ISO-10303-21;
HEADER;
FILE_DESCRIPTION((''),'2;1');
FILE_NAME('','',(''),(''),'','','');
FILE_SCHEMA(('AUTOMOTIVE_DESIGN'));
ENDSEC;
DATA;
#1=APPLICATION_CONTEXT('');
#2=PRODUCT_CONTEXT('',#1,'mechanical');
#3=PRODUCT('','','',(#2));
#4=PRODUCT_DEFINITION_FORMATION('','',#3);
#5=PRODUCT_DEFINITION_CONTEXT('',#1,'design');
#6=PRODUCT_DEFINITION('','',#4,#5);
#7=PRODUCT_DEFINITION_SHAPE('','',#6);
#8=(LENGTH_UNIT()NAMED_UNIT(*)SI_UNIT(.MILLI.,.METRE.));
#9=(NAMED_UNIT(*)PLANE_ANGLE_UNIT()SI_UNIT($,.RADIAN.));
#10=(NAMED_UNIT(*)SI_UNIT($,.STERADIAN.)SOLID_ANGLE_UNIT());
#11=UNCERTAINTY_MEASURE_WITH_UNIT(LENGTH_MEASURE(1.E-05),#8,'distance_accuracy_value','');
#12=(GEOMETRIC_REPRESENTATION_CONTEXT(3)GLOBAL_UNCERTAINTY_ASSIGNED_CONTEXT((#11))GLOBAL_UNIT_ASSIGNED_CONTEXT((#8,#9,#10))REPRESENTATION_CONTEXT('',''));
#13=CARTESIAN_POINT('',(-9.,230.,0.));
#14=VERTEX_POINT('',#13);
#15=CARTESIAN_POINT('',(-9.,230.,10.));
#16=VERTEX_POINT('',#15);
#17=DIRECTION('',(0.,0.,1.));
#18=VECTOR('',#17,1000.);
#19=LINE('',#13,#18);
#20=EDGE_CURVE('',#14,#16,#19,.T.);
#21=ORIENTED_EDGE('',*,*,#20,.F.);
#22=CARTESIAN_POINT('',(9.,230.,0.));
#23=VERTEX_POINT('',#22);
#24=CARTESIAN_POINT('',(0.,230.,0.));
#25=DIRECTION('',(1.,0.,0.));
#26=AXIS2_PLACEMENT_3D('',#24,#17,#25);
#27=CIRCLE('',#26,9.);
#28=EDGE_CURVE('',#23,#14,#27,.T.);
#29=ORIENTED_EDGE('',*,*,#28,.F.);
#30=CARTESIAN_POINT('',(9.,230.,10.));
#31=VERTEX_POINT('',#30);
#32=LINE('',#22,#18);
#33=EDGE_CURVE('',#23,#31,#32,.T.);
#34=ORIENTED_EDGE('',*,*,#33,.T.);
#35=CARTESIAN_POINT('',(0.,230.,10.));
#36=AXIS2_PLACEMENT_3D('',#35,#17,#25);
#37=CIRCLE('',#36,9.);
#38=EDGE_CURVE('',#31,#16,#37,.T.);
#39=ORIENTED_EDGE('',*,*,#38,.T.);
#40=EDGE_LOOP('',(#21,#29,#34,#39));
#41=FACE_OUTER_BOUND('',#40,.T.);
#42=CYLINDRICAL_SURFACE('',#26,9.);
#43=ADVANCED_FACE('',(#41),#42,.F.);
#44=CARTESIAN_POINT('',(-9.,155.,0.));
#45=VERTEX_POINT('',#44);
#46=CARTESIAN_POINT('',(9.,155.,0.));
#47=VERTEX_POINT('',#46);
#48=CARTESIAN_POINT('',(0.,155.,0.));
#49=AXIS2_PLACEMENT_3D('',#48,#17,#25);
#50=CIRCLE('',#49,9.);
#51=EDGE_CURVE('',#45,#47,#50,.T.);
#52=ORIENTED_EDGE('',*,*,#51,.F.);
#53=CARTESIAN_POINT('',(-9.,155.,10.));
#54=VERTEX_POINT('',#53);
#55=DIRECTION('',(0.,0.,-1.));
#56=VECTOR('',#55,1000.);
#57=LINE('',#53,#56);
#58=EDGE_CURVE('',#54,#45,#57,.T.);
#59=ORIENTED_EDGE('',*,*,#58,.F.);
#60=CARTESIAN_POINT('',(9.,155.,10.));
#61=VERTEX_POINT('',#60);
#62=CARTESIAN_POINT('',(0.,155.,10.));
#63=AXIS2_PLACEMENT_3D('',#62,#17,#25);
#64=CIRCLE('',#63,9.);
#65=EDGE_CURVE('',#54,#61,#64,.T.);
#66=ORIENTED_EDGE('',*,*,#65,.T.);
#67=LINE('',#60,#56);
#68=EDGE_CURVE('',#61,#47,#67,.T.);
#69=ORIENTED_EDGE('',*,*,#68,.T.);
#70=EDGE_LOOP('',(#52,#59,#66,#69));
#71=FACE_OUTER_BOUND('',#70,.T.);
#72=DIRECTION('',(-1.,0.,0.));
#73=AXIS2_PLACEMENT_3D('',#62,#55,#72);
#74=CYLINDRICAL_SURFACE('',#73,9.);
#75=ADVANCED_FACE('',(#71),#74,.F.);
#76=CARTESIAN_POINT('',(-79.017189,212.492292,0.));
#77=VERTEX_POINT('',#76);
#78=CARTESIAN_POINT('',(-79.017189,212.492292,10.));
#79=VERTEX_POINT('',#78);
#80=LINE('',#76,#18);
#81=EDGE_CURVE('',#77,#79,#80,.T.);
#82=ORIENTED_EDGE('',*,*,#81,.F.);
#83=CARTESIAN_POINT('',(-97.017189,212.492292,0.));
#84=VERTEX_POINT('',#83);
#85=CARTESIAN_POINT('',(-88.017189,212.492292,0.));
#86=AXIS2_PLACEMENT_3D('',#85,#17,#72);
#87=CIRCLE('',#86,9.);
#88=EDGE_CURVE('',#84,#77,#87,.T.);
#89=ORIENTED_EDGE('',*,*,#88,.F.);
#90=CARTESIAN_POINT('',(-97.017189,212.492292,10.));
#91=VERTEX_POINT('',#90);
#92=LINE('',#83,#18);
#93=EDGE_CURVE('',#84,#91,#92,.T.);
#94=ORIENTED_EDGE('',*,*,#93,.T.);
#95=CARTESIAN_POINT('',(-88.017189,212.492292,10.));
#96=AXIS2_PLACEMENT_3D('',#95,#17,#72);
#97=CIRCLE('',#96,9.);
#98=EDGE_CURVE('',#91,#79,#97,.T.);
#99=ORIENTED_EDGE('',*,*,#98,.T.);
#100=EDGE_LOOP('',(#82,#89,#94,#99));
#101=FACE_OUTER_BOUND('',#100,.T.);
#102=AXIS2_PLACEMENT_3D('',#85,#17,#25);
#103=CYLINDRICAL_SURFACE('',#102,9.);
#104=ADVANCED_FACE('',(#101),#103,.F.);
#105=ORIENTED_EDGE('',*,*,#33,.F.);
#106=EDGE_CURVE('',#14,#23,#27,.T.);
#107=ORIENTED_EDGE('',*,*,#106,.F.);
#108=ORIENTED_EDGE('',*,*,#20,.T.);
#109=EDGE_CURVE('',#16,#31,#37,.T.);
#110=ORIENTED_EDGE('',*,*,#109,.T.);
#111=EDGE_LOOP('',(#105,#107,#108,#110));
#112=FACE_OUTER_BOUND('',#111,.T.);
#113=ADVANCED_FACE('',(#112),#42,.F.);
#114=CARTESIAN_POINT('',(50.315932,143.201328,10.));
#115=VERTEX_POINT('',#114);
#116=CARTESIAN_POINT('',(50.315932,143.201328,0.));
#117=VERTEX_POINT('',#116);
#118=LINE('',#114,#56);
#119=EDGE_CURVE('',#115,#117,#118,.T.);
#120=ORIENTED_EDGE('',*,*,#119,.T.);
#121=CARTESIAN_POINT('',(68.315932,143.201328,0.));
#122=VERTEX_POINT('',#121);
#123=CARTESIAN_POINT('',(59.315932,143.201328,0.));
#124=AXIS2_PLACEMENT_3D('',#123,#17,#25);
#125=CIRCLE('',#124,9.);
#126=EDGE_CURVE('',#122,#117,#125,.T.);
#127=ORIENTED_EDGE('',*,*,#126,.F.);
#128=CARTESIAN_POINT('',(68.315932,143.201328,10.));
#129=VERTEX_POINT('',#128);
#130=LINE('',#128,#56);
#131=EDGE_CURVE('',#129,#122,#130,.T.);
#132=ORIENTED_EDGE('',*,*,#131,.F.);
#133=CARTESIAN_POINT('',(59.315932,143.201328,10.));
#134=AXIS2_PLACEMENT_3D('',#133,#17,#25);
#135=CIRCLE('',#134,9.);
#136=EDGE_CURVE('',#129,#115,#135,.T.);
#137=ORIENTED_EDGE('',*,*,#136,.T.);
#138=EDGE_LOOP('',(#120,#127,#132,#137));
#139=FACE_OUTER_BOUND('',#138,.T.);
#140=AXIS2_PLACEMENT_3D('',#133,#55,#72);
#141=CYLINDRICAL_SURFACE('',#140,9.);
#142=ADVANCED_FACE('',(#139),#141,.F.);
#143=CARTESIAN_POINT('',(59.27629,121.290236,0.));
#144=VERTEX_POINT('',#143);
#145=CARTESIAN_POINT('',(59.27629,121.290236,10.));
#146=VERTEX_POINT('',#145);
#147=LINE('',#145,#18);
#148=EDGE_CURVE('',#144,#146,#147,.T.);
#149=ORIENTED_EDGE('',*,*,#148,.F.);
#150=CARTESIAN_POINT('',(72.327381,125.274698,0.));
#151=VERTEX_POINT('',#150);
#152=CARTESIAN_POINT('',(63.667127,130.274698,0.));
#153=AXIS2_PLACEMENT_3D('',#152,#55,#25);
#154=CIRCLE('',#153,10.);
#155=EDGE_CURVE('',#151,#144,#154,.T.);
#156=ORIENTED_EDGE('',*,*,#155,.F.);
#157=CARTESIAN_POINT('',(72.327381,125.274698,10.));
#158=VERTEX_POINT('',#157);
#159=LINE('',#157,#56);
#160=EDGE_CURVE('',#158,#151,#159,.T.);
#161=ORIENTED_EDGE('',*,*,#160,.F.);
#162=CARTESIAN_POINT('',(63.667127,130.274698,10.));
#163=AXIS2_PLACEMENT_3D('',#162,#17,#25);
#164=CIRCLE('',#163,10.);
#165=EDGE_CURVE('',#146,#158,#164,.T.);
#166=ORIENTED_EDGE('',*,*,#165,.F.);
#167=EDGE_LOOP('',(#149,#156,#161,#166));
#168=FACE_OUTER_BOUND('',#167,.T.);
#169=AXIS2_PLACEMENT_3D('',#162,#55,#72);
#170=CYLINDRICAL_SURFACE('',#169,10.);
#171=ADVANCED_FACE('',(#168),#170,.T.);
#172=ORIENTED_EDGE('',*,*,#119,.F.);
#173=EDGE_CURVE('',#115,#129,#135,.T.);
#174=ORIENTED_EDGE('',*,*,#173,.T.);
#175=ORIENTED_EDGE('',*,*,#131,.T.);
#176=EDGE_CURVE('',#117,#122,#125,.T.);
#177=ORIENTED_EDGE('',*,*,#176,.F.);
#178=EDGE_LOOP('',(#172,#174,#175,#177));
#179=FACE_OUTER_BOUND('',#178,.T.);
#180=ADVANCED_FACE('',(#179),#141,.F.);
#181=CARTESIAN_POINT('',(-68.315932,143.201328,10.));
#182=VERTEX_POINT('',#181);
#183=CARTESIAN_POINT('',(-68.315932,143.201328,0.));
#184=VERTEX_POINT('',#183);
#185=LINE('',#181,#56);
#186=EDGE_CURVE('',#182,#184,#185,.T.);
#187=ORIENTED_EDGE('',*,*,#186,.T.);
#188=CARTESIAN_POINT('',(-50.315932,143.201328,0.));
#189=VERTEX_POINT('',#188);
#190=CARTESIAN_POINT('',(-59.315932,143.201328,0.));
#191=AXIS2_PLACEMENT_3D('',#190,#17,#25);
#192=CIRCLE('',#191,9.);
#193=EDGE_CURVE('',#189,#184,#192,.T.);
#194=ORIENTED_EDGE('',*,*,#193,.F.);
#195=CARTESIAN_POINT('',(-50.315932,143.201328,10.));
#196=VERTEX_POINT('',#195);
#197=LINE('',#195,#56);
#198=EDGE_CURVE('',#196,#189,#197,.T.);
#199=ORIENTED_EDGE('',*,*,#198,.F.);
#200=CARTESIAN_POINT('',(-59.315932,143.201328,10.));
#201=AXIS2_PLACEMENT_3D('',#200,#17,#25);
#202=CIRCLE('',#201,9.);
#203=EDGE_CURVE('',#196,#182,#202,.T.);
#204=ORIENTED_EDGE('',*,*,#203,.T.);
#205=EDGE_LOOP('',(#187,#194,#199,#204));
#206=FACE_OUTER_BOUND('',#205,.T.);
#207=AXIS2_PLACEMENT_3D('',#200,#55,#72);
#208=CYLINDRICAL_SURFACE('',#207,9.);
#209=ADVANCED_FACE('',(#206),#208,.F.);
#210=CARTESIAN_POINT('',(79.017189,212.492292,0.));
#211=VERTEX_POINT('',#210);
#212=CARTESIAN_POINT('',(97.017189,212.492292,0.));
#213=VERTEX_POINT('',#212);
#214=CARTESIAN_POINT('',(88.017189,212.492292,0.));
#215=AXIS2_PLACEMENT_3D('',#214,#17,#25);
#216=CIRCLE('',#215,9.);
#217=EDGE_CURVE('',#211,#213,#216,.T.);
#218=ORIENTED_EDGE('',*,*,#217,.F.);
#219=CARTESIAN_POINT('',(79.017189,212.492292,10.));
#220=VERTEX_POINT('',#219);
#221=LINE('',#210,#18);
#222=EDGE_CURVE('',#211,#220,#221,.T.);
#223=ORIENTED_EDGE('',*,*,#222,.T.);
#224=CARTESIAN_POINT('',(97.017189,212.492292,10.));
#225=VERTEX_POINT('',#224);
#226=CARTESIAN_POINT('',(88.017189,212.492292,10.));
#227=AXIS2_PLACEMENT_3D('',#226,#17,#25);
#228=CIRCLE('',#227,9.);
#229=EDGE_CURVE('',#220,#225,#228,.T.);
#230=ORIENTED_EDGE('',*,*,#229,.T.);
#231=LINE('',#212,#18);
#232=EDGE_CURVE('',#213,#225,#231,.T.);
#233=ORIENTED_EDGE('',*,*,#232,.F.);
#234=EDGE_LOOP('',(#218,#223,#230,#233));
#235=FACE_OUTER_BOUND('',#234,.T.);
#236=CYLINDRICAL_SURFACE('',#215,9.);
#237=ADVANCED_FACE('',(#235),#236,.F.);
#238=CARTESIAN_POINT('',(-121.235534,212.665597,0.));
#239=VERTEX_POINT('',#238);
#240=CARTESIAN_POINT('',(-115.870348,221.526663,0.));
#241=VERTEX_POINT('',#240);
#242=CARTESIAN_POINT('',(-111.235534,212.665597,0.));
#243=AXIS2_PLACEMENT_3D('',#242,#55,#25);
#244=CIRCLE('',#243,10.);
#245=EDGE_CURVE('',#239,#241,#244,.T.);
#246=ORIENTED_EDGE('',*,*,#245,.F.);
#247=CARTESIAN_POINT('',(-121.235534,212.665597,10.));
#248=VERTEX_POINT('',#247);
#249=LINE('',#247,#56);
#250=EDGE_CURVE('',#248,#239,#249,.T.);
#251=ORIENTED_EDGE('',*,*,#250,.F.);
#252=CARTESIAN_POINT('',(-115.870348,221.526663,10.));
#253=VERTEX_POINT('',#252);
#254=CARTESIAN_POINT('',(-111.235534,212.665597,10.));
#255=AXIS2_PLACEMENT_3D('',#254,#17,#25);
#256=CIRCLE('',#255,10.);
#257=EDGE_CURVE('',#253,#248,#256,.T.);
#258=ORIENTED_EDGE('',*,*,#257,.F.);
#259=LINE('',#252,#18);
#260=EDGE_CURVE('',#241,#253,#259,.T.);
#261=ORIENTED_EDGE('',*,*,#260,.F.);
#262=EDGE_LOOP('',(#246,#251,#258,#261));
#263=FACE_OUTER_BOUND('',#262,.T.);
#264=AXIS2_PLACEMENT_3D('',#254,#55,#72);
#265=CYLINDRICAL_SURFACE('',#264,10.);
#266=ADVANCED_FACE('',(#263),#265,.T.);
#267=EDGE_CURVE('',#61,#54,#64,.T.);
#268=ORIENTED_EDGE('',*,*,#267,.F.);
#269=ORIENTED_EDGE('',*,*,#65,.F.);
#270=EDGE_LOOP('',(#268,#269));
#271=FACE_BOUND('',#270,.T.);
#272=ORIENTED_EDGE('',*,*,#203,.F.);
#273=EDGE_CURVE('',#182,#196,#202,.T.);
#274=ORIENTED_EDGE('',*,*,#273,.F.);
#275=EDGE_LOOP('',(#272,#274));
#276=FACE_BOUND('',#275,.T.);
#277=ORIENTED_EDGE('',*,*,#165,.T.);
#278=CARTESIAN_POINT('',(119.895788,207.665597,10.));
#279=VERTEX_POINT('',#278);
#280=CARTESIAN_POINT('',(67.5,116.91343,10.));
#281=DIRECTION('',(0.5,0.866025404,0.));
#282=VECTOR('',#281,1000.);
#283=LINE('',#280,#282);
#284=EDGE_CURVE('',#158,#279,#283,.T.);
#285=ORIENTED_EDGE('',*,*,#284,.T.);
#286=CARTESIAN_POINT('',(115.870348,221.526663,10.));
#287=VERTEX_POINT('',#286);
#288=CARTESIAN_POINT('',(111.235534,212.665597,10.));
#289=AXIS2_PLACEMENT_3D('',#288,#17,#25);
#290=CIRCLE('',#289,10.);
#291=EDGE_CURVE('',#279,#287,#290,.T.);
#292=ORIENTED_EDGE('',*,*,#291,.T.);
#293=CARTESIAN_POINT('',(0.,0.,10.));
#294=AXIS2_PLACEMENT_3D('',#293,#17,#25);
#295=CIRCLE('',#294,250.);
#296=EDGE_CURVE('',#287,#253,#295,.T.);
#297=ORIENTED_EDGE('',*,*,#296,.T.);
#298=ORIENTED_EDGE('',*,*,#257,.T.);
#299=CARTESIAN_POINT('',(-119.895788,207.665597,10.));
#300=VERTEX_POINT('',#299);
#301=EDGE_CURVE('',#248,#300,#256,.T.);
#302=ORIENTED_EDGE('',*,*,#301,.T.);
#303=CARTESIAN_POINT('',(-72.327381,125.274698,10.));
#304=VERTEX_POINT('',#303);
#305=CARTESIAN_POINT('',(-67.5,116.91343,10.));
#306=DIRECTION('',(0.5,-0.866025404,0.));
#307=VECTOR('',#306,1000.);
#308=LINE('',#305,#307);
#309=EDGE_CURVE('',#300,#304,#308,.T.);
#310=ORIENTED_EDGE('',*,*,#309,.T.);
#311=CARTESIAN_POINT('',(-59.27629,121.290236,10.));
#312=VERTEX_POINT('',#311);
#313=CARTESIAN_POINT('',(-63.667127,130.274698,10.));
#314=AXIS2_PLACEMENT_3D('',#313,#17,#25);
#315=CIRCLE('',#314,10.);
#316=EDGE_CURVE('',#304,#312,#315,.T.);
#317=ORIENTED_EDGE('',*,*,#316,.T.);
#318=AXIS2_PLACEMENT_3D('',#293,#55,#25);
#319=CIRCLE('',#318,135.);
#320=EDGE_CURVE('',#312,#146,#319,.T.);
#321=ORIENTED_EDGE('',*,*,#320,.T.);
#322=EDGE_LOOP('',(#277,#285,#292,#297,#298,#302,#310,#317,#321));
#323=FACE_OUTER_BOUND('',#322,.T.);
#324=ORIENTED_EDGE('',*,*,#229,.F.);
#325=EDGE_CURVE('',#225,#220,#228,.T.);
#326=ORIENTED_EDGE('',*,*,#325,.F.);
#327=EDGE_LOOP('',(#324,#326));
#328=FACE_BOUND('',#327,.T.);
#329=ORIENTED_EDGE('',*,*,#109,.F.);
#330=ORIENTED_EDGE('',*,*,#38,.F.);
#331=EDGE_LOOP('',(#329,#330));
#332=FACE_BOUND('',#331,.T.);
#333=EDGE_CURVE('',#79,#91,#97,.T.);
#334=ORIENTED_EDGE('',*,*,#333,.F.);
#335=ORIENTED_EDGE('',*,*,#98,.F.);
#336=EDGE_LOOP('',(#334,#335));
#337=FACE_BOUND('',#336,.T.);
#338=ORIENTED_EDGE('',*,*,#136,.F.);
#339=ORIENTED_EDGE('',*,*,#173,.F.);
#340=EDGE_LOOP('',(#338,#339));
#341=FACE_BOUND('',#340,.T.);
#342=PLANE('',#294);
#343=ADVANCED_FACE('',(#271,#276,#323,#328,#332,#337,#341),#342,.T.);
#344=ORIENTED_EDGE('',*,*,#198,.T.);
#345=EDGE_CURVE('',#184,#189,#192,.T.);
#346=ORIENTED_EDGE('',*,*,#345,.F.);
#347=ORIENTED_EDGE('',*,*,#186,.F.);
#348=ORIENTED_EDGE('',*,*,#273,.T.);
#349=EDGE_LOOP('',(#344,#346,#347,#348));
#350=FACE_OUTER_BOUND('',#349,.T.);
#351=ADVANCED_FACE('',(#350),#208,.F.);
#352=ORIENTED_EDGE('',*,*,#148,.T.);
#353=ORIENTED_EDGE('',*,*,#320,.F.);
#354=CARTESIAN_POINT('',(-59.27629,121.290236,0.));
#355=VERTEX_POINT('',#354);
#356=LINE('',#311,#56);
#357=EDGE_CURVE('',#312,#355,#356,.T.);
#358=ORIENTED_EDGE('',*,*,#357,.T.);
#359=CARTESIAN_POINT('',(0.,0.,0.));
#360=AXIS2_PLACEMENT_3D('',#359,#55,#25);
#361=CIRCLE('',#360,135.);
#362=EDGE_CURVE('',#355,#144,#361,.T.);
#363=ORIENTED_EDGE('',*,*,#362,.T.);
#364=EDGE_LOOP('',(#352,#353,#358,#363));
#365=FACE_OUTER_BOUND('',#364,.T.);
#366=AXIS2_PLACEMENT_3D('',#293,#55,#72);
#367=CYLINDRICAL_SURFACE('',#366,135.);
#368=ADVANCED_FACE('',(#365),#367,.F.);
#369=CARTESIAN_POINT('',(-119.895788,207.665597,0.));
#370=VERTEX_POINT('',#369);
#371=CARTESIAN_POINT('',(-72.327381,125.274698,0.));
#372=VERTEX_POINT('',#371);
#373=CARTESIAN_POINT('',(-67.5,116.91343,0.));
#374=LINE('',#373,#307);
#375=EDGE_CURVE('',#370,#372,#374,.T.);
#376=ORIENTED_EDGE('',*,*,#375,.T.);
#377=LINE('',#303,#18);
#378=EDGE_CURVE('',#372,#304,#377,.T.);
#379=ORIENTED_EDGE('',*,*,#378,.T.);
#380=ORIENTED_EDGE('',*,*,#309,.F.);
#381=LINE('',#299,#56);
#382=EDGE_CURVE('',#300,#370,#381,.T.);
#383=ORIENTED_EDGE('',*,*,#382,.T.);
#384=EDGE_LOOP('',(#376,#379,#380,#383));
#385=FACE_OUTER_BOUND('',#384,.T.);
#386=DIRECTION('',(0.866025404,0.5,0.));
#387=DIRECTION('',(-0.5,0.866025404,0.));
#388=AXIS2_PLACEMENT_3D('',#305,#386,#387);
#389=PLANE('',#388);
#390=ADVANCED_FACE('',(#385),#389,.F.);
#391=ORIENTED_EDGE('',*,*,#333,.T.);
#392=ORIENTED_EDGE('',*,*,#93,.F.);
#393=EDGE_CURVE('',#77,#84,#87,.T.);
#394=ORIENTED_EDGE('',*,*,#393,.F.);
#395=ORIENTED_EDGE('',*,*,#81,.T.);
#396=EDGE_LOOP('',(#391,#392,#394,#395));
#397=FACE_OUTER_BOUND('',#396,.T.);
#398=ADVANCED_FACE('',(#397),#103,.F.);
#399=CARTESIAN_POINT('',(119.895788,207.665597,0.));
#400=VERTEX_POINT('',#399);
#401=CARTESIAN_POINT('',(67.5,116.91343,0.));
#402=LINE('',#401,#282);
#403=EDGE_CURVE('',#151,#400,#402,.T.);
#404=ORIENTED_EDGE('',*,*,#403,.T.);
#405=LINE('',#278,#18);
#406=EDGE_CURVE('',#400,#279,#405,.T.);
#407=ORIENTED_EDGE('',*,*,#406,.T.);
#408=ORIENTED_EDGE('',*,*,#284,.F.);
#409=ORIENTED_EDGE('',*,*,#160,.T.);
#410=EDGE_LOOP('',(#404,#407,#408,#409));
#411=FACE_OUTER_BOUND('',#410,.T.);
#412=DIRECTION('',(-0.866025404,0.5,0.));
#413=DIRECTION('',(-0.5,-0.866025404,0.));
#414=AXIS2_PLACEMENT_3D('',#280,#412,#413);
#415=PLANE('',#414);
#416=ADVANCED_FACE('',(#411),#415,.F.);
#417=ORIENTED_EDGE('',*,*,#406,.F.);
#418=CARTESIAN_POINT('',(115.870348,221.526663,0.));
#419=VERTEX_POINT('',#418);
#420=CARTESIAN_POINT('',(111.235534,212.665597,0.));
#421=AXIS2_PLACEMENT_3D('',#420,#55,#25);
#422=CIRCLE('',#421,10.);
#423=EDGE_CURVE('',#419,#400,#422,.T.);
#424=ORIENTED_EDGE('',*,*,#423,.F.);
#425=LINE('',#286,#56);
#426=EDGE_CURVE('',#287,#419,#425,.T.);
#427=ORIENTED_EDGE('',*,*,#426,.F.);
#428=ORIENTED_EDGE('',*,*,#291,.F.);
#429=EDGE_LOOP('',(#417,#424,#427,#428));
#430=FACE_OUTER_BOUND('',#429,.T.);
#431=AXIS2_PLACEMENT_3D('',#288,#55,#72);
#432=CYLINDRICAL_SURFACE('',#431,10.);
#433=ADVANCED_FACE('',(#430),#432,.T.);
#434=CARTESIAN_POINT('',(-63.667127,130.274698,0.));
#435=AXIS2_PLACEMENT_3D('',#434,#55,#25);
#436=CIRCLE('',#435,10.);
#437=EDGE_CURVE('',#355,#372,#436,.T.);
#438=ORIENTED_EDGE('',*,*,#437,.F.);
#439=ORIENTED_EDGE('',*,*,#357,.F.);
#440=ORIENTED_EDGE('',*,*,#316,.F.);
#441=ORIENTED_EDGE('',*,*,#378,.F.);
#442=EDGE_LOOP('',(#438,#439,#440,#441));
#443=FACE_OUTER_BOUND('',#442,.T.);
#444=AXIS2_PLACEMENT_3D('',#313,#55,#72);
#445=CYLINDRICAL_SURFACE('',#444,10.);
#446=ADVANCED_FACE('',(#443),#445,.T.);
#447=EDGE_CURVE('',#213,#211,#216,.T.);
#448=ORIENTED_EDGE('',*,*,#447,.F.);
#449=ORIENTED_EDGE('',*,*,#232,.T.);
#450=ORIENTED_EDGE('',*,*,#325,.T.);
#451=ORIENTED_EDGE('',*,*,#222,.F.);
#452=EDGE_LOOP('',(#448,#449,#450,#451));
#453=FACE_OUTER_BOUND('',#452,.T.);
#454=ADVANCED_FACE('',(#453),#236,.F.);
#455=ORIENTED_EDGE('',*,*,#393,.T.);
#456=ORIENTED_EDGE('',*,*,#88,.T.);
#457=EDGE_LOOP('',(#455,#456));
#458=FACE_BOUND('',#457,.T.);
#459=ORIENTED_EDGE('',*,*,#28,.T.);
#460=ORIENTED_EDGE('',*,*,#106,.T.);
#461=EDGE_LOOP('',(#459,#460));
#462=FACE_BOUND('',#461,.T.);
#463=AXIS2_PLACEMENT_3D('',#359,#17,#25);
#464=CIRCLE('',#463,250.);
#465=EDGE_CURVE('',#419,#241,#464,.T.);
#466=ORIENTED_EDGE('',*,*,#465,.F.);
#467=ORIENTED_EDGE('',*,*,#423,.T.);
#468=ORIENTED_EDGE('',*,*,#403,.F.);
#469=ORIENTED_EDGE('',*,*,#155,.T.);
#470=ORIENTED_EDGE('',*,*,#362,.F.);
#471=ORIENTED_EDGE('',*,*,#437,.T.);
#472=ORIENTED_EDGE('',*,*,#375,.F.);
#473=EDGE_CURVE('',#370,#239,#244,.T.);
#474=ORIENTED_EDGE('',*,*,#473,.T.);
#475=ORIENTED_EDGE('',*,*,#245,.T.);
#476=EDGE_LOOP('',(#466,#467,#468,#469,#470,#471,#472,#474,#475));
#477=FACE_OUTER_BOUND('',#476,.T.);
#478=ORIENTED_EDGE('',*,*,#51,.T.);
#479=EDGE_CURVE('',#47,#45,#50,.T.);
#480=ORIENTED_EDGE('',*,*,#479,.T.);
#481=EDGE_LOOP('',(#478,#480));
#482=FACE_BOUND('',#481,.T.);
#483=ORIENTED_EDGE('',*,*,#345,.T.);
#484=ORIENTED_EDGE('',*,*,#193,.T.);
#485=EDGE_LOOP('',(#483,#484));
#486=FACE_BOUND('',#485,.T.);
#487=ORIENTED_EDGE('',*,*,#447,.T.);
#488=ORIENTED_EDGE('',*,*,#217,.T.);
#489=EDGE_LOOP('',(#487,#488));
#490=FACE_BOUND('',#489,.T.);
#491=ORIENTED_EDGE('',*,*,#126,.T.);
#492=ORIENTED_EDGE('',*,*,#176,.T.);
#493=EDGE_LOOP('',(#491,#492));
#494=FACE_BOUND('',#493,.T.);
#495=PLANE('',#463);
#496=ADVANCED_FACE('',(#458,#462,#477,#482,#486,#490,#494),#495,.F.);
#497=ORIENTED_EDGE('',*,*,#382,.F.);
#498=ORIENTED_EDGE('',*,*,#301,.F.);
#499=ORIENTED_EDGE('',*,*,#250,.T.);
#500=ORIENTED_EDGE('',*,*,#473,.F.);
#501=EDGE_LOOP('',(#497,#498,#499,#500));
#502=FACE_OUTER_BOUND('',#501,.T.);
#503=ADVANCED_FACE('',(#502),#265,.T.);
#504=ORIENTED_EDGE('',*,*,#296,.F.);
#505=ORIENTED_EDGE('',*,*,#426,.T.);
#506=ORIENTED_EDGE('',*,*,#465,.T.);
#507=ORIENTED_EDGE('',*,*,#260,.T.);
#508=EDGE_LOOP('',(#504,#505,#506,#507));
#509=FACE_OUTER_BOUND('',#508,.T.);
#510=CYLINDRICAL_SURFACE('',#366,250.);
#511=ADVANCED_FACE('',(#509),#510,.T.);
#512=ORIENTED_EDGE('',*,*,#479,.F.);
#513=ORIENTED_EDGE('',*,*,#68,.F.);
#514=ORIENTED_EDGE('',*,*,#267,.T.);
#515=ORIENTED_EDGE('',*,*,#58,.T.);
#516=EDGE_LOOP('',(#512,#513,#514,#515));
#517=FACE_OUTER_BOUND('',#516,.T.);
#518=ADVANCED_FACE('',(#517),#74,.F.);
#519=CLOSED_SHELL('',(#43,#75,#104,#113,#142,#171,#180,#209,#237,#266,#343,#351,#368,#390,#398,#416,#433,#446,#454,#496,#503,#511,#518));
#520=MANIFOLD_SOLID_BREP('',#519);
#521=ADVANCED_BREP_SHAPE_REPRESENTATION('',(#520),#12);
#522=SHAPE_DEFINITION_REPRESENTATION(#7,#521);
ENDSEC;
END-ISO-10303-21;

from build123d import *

# Parameters (mm, degrees)
SKETCH_1_R          = 9
EXTRUDE_1_DEPTH     = 10
FILLET_1_R          = 10
SKETCH_2_R          = 9
CUT_EXTRUDE_1_DEPTH = 279.025277116


with BuildPart() as part:
    # 草图1 → 凸台-拉伸1 (new body)
    with BuildSketch(Plane.XY):
        with BuildLine():
            Line((-67.5, 116.913429511), (-125, 216.506350946))
            ThreePointArc((-125, 216.506350946), (0, 250), (125, 216.506350946))
            Line((125, 216.506350946), (67.5, 116.913429511))
            ThreePointArc((67.5, 116.913429511), (0, 135), (-67.5, 116.913429511))
        make_face()
        with Locations((0, 155)):
            Circle(SKETCH_1_R, mode=Mode.SUBTRACT)
        with Locations((59.315932017, 143.201327539)):
            Circle(SKETCH_1_R, mode=Mode.SUBTRACT)
        with Locations((-59.315932017, 143.201327539)):
            Circle(SKETCH_1_R, mode=Mode.SUBTRACT)
    extrude(amount=EXTRUDE_1_DEPTH)

    # 圆角1
    fillet_1_edges = [part.edges().sort_by_distance(p)[0] for p in [
        (-67.5, 116.913429511, 5),
        (-125, 216.506350946, 5),
        (125, 216.506350946, 5),
        (67.5, 116.913429511, 5),
    ]]
    fillet(fillet_1_edges, radius=FILLET_1_R)

    # 草图2 → 切除-拉伸1 (cut, through all)
    with BuildSketch(Plane.XY.offset(10)):
        with Locations((0, 230)):
            Circle(SKETCH_2_R)
        with Locations((88.017189444, 212.492292478)):
            Circle(SKETCH_2_R)
        with Locations(Location((-88.017189444, 212.492292478, 0), (0, 0, 180))):
            Circle(SKETCH_2_R)
    extrude(amount=-CUT_EXTRUDE_1_DEPTH, mode=Mode.SUBTRACT)


solid = part.part
